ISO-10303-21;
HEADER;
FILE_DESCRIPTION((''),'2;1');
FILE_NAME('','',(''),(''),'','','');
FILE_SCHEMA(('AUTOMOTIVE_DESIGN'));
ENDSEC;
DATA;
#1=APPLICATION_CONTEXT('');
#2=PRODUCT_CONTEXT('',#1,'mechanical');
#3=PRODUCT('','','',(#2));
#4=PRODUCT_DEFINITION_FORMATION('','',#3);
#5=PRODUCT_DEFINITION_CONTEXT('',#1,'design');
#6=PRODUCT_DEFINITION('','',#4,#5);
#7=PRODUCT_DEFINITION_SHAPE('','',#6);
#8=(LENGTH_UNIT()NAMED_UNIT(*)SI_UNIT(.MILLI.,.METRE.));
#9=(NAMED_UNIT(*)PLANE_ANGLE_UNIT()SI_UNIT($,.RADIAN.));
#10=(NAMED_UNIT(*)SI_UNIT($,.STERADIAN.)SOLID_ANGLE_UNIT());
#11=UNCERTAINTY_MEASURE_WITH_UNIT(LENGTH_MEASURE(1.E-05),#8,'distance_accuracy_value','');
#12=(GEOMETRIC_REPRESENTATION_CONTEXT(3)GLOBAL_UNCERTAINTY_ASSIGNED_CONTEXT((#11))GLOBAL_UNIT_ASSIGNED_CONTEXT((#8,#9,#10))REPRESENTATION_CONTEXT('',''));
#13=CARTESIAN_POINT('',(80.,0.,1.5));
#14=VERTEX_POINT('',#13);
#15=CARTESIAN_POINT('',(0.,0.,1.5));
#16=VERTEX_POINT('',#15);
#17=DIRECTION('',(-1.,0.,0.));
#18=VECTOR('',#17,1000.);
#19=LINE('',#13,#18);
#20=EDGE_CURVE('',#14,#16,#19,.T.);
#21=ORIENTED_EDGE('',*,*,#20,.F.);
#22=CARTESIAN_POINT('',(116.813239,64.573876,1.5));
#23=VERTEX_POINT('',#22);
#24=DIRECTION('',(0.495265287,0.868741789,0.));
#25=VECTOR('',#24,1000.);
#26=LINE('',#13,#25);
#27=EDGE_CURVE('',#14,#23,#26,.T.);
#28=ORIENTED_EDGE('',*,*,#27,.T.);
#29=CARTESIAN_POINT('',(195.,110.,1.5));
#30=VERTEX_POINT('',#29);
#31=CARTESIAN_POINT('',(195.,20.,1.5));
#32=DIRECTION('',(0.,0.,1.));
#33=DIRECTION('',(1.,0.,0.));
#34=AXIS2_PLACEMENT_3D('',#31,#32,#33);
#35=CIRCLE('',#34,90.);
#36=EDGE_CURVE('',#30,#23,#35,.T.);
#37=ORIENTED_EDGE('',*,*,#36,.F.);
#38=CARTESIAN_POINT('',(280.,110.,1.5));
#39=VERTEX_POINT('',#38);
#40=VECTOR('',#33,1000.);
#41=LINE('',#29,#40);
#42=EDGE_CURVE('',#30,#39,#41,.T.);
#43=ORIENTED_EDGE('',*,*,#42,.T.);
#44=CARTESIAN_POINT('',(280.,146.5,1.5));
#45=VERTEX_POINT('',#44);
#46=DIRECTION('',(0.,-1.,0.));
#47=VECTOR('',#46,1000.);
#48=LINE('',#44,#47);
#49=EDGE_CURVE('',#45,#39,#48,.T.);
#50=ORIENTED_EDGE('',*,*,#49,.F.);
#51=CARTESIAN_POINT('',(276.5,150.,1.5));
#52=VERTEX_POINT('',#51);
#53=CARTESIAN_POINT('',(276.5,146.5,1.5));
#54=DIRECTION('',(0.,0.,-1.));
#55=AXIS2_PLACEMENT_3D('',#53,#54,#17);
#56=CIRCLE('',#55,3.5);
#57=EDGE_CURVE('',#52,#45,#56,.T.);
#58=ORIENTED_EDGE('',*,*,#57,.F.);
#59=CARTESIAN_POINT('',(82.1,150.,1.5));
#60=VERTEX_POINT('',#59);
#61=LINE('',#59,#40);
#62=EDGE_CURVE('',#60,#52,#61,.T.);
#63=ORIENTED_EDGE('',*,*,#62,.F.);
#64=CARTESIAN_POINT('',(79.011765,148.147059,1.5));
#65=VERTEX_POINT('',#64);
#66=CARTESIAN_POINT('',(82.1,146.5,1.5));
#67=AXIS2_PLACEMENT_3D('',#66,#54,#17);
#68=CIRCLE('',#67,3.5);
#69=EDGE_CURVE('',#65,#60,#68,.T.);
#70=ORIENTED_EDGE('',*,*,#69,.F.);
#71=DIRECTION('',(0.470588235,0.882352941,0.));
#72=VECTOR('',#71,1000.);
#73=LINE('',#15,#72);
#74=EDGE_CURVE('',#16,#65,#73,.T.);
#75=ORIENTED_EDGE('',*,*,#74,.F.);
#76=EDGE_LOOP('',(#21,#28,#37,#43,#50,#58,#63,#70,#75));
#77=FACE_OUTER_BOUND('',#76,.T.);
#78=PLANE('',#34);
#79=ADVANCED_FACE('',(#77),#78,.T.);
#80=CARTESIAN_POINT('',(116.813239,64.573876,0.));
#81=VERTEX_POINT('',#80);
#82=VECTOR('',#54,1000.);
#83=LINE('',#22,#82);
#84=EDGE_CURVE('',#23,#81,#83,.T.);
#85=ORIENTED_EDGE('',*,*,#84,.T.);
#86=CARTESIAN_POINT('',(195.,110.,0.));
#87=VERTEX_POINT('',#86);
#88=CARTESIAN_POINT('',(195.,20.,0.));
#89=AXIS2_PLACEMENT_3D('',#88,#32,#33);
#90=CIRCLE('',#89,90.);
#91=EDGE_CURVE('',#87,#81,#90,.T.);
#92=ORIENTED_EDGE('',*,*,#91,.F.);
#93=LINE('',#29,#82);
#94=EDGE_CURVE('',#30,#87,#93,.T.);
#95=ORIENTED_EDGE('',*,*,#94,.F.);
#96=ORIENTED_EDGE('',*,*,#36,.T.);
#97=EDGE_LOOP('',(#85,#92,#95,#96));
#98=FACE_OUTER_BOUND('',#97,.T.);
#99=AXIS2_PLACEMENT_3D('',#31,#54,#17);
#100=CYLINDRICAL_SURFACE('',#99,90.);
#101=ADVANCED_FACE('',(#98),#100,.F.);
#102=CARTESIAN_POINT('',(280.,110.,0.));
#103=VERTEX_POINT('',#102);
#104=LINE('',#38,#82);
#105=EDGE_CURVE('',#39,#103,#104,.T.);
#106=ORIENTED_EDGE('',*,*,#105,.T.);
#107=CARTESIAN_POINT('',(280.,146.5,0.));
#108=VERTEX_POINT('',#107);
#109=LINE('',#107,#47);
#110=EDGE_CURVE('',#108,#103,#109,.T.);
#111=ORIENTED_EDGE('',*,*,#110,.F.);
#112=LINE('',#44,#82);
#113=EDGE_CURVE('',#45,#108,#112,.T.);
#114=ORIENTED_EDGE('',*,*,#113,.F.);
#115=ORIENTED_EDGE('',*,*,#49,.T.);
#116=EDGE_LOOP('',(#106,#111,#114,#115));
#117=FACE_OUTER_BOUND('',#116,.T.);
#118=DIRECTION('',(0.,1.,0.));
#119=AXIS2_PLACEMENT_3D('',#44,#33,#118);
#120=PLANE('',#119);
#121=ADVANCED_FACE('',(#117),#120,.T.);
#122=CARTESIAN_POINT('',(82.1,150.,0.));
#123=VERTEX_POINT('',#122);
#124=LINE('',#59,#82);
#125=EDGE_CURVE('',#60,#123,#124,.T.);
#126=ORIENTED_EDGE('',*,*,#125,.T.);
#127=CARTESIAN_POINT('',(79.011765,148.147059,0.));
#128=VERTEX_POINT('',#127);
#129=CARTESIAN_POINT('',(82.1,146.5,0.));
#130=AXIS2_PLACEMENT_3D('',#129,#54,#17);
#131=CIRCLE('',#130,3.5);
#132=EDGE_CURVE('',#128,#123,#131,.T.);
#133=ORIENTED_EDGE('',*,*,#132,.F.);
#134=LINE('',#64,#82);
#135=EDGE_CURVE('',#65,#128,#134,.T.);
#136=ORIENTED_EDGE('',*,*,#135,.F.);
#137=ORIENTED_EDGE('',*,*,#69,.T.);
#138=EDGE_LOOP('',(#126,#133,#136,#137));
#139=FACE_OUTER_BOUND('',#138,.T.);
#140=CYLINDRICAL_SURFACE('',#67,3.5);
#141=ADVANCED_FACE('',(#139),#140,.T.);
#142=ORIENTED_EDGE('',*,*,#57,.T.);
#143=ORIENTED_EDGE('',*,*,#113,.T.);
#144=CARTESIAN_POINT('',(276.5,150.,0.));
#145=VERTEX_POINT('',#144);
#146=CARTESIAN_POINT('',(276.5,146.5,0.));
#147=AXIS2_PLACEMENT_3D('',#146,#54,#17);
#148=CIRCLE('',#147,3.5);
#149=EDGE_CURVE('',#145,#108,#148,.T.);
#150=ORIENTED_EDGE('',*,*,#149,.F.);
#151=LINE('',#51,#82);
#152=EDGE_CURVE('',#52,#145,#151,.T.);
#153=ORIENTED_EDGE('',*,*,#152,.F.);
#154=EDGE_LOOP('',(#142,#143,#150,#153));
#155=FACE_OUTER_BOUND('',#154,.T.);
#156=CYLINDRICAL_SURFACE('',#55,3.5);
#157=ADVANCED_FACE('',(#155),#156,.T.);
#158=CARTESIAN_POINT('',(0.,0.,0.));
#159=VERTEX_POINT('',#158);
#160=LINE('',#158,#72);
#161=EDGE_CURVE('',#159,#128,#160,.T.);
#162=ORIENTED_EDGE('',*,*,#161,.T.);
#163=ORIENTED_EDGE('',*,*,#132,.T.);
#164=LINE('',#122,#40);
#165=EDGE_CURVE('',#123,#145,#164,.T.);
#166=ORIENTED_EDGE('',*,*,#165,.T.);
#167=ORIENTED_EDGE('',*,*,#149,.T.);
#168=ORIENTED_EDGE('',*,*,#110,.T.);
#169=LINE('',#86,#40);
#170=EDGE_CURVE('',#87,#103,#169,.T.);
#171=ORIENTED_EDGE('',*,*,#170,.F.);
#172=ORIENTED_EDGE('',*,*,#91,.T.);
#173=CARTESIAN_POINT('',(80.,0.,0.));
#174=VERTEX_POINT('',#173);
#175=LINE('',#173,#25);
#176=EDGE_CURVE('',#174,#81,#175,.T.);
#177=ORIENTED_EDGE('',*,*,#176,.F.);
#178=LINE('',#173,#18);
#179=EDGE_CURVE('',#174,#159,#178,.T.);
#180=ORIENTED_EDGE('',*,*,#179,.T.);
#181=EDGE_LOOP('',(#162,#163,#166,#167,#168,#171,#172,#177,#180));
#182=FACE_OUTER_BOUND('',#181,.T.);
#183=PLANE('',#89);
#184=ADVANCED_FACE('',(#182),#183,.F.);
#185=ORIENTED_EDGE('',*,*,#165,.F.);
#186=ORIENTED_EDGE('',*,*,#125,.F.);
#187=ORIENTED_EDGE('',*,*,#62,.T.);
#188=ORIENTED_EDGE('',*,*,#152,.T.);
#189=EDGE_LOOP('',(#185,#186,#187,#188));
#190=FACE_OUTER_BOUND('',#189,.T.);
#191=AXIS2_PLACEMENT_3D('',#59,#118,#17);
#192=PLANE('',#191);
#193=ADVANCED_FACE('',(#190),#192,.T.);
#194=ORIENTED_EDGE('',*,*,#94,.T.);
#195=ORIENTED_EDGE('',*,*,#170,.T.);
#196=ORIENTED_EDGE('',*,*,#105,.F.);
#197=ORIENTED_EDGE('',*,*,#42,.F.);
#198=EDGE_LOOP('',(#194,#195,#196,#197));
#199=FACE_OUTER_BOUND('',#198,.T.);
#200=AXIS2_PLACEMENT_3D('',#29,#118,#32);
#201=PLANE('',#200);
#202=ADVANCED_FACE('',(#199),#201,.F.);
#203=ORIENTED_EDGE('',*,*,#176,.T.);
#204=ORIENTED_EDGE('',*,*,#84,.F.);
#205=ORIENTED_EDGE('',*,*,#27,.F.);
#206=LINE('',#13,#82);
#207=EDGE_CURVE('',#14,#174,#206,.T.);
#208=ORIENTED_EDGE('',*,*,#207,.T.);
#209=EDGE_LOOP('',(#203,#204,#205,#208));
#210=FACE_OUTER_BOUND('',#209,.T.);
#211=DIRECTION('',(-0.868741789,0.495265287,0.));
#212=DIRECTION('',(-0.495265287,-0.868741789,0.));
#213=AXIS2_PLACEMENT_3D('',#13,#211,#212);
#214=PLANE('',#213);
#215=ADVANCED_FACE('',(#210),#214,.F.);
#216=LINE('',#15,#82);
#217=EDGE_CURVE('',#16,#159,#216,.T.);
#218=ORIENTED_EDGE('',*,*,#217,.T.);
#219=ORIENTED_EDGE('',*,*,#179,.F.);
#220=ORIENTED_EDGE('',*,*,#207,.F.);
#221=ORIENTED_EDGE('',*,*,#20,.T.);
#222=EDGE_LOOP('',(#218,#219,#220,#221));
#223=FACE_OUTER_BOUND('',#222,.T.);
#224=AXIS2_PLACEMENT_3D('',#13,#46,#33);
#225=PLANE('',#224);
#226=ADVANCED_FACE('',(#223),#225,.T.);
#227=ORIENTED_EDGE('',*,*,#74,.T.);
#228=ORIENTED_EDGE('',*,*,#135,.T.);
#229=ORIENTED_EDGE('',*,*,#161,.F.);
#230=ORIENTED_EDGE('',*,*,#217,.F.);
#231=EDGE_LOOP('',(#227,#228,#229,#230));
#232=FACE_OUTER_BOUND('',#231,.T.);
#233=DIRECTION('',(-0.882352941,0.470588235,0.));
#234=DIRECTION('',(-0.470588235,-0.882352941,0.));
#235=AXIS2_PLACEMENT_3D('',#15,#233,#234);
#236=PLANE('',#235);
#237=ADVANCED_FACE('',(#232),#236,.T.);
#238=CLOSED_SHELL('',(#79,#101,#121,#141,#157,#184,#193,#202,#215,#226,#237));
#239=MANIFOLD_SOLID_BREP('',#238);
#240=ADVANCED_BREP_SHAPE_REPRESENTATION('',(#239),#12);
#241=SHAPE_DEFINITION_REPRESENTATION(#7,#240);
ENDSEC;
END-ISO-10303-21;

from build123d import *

# Parameters (mm, degrees)
BOSS_EXTRUDE1_DEPTH = 1.5


with BuildPart() as part:
    # Sketch1 → Boss-Extrude1 (new body)
    with BuildSketch(Plane.XY):
        with BuildLine():
            Line((0, 0), (79.011764706, 148.147058824))
            ThreePointArc((79.011764706, 148.147058824), (80.299264856, 149.50122524), (82.1, 150))
            Line((82.1, 150), (276.5, 150))
            ThreePointArc((276.5, 150), (278.974873734, 148.974873734), (280, 146.5))
            Line((280, 146.5), (280, 110))
            Line((280, 110), (195, 110))
            ThreePointArc((195, 110), (149.787439916, 97.819177653), (116.813238993, 64.573875793))
            Line((116.813238993, 64.573875793), (80, 0))
            Line((80, 0), (0, 0))
        make_face()
    extrude(amount=BOSS_EXTRUDE1_DEPTH)


solid = part.part
